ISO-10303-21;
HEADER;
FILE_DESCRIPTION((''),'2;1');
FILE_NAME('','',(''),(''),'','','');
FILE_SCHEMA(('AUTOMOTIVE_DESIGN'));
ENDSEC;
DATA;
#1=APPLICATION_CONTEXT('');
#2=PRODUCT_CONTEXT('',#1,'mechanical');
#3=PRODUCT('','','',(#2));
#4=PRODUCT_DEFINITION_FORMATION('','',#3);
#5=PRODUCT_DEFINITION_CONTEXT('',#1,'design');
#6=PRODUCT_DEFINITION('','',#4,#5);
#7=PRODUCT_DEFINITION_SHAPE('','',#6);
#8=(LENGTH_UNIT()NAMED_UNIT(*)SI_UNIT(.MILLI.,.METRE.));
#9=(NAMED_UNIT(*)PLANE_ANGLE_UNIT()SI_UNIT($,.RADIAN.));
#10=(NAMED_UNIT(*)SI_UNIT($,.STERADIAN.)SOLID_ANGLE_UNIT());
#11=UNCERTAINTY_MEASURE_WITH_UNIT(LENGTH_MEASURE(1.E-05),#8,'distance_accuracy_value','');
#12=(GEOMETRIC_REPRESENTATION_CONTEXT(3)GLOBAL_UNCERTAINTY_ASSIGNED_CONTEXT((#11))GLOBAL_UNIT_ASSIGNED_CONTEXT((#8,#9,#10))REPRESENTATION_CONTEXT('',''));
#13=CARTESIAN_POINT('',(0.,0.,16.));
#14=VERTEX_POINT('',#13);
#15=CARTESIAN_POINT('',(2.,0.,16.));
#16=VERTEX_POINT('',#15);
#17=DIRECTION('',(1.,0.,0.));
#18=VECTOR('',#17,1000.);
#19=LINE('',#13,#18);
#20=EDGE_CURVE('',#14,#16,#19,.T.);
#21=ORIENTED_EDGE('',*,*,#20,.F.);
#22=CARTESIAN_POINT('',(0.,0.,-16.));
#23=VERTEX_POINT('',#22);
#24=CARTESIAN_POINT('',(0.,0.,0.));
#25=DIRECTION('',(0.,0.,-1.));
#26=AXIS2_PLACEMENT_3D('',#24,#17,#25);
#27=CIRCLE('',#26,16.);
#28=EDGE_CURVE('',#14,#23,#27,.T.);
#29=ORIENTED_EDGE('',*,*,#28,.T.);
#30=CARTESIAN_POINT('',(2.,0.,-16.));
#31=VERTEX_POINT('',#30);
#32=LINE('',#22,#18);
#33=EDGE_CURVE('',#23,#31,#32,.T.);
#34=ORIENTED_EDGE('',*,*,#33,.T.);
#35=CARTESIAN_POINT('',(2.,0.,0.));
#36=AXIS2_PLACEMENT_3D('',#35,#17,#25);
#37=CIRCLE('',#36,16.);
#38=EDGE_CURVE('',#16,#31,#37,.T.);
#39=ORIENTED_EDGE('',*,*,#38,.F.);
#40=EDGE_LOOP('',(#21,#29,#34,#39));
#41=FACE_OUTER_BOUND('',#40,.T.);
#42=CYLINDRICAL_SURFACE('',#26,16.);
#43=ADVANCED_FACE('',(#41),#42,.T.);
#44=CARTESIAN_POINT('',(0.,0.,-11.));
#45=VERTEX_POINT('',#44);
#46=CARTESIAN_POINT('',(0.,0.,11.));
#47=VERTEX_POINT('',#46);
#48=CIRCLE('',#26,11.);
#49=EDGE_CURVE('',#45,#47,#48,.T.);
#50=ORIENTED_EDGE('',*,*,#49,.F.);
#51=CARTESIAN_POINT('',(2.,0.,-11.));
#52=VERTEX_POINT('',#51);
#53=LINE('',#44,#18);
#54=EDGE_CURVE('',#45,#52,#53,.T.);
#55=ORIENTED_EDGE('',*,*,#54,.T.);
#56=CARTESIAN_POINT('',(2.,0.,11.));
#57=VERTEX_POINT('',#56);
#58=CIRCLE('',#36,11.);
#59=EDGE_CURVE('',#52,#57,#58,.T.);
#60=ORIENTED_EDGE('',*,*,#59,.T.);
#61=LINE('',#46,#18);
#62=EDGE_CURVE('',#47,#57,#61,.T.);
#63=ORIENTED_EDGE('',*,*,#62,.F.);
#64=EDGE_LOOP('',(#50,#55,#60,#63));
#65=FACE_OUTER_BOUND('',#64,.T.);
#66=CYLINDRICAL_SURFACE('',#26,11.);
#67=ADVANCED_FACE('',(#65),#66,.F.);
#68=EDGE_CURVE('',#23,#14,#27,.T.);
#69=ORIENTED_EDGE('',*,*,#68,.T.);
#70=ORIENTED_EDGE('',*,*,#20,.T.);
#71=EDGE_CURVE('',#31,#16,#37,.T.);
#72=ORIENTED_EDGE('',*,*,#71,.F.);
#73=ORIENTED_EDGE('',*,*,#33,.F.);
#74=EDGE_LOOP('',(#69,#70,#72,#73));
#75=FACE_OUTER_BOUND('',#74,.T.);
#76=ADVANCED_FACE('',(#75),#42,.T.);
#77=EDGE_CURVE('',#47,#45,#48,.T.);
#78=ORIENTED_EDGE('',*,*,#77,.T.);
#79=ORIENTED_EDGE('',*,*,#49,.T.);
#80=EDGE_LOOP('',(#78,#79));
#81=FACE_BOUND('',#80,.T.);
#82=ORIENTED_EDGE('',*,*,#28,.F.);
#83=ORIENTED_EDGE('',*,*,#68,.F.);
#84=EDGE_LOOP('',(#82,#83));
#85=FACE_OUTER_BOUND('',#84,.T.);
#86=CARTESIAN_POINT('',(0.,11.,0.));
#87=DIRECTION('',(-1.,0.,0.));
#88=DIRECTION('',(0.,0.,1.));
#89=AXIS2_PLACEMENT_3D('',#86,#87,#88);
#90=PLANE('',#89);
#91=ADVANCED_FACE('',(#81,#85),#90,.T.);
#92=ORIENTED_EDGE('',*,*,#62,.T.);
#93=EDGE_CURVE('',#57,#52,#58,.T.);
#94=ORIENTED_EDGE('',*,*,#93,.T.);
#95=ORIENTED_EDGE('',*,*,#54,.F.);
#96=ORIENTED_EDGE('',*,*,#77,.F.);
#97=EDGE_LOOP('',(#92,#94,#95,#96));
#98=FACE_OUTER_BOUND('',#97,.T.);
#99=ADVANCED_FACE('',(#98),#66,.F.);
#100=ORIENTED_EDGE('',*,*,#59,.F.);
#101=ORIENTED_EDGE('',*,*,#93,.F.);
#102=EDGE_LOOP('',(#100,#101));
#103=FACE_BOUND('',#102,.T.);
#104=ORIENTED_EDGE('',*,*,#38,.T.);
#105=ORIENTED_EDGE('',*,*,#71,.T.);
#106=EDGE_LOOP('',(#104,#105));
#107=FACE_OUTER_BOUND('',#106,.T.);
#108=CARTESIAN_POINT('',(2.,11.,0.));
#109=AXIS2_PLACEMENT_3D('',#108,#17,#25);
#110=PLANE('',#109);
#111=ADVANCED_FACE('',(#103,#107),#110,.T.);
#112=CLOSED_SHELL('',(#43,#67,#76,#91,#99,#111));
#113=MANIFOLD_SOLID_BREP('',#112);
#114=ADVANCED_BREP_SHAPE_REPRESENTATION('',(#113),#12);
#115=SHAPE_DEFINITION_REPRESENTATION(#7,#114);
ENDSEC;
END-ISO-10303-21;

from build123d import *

# Parameters (mm, degrees)
SKETCH1_W = 2
SKETCH1_H = 5


with BuildPart() as part:
    # Sketch1 → Revolve1 (revolve)
    with BuildSketch(Plane.XY, mode=Mode.PRIVATE) as revolve1_sk:
        with Locations((1, 13.5)):
            Rectangle(SKETCH1_W, SKETCH1_H)
    revolve(revolve1_sk.sketch.rotate(Axis((0, 0, 0), (-1, 0, 0)), 90), axis=Axis((0, 0, 0), (-1, 0, 0)))


solid = part.part
